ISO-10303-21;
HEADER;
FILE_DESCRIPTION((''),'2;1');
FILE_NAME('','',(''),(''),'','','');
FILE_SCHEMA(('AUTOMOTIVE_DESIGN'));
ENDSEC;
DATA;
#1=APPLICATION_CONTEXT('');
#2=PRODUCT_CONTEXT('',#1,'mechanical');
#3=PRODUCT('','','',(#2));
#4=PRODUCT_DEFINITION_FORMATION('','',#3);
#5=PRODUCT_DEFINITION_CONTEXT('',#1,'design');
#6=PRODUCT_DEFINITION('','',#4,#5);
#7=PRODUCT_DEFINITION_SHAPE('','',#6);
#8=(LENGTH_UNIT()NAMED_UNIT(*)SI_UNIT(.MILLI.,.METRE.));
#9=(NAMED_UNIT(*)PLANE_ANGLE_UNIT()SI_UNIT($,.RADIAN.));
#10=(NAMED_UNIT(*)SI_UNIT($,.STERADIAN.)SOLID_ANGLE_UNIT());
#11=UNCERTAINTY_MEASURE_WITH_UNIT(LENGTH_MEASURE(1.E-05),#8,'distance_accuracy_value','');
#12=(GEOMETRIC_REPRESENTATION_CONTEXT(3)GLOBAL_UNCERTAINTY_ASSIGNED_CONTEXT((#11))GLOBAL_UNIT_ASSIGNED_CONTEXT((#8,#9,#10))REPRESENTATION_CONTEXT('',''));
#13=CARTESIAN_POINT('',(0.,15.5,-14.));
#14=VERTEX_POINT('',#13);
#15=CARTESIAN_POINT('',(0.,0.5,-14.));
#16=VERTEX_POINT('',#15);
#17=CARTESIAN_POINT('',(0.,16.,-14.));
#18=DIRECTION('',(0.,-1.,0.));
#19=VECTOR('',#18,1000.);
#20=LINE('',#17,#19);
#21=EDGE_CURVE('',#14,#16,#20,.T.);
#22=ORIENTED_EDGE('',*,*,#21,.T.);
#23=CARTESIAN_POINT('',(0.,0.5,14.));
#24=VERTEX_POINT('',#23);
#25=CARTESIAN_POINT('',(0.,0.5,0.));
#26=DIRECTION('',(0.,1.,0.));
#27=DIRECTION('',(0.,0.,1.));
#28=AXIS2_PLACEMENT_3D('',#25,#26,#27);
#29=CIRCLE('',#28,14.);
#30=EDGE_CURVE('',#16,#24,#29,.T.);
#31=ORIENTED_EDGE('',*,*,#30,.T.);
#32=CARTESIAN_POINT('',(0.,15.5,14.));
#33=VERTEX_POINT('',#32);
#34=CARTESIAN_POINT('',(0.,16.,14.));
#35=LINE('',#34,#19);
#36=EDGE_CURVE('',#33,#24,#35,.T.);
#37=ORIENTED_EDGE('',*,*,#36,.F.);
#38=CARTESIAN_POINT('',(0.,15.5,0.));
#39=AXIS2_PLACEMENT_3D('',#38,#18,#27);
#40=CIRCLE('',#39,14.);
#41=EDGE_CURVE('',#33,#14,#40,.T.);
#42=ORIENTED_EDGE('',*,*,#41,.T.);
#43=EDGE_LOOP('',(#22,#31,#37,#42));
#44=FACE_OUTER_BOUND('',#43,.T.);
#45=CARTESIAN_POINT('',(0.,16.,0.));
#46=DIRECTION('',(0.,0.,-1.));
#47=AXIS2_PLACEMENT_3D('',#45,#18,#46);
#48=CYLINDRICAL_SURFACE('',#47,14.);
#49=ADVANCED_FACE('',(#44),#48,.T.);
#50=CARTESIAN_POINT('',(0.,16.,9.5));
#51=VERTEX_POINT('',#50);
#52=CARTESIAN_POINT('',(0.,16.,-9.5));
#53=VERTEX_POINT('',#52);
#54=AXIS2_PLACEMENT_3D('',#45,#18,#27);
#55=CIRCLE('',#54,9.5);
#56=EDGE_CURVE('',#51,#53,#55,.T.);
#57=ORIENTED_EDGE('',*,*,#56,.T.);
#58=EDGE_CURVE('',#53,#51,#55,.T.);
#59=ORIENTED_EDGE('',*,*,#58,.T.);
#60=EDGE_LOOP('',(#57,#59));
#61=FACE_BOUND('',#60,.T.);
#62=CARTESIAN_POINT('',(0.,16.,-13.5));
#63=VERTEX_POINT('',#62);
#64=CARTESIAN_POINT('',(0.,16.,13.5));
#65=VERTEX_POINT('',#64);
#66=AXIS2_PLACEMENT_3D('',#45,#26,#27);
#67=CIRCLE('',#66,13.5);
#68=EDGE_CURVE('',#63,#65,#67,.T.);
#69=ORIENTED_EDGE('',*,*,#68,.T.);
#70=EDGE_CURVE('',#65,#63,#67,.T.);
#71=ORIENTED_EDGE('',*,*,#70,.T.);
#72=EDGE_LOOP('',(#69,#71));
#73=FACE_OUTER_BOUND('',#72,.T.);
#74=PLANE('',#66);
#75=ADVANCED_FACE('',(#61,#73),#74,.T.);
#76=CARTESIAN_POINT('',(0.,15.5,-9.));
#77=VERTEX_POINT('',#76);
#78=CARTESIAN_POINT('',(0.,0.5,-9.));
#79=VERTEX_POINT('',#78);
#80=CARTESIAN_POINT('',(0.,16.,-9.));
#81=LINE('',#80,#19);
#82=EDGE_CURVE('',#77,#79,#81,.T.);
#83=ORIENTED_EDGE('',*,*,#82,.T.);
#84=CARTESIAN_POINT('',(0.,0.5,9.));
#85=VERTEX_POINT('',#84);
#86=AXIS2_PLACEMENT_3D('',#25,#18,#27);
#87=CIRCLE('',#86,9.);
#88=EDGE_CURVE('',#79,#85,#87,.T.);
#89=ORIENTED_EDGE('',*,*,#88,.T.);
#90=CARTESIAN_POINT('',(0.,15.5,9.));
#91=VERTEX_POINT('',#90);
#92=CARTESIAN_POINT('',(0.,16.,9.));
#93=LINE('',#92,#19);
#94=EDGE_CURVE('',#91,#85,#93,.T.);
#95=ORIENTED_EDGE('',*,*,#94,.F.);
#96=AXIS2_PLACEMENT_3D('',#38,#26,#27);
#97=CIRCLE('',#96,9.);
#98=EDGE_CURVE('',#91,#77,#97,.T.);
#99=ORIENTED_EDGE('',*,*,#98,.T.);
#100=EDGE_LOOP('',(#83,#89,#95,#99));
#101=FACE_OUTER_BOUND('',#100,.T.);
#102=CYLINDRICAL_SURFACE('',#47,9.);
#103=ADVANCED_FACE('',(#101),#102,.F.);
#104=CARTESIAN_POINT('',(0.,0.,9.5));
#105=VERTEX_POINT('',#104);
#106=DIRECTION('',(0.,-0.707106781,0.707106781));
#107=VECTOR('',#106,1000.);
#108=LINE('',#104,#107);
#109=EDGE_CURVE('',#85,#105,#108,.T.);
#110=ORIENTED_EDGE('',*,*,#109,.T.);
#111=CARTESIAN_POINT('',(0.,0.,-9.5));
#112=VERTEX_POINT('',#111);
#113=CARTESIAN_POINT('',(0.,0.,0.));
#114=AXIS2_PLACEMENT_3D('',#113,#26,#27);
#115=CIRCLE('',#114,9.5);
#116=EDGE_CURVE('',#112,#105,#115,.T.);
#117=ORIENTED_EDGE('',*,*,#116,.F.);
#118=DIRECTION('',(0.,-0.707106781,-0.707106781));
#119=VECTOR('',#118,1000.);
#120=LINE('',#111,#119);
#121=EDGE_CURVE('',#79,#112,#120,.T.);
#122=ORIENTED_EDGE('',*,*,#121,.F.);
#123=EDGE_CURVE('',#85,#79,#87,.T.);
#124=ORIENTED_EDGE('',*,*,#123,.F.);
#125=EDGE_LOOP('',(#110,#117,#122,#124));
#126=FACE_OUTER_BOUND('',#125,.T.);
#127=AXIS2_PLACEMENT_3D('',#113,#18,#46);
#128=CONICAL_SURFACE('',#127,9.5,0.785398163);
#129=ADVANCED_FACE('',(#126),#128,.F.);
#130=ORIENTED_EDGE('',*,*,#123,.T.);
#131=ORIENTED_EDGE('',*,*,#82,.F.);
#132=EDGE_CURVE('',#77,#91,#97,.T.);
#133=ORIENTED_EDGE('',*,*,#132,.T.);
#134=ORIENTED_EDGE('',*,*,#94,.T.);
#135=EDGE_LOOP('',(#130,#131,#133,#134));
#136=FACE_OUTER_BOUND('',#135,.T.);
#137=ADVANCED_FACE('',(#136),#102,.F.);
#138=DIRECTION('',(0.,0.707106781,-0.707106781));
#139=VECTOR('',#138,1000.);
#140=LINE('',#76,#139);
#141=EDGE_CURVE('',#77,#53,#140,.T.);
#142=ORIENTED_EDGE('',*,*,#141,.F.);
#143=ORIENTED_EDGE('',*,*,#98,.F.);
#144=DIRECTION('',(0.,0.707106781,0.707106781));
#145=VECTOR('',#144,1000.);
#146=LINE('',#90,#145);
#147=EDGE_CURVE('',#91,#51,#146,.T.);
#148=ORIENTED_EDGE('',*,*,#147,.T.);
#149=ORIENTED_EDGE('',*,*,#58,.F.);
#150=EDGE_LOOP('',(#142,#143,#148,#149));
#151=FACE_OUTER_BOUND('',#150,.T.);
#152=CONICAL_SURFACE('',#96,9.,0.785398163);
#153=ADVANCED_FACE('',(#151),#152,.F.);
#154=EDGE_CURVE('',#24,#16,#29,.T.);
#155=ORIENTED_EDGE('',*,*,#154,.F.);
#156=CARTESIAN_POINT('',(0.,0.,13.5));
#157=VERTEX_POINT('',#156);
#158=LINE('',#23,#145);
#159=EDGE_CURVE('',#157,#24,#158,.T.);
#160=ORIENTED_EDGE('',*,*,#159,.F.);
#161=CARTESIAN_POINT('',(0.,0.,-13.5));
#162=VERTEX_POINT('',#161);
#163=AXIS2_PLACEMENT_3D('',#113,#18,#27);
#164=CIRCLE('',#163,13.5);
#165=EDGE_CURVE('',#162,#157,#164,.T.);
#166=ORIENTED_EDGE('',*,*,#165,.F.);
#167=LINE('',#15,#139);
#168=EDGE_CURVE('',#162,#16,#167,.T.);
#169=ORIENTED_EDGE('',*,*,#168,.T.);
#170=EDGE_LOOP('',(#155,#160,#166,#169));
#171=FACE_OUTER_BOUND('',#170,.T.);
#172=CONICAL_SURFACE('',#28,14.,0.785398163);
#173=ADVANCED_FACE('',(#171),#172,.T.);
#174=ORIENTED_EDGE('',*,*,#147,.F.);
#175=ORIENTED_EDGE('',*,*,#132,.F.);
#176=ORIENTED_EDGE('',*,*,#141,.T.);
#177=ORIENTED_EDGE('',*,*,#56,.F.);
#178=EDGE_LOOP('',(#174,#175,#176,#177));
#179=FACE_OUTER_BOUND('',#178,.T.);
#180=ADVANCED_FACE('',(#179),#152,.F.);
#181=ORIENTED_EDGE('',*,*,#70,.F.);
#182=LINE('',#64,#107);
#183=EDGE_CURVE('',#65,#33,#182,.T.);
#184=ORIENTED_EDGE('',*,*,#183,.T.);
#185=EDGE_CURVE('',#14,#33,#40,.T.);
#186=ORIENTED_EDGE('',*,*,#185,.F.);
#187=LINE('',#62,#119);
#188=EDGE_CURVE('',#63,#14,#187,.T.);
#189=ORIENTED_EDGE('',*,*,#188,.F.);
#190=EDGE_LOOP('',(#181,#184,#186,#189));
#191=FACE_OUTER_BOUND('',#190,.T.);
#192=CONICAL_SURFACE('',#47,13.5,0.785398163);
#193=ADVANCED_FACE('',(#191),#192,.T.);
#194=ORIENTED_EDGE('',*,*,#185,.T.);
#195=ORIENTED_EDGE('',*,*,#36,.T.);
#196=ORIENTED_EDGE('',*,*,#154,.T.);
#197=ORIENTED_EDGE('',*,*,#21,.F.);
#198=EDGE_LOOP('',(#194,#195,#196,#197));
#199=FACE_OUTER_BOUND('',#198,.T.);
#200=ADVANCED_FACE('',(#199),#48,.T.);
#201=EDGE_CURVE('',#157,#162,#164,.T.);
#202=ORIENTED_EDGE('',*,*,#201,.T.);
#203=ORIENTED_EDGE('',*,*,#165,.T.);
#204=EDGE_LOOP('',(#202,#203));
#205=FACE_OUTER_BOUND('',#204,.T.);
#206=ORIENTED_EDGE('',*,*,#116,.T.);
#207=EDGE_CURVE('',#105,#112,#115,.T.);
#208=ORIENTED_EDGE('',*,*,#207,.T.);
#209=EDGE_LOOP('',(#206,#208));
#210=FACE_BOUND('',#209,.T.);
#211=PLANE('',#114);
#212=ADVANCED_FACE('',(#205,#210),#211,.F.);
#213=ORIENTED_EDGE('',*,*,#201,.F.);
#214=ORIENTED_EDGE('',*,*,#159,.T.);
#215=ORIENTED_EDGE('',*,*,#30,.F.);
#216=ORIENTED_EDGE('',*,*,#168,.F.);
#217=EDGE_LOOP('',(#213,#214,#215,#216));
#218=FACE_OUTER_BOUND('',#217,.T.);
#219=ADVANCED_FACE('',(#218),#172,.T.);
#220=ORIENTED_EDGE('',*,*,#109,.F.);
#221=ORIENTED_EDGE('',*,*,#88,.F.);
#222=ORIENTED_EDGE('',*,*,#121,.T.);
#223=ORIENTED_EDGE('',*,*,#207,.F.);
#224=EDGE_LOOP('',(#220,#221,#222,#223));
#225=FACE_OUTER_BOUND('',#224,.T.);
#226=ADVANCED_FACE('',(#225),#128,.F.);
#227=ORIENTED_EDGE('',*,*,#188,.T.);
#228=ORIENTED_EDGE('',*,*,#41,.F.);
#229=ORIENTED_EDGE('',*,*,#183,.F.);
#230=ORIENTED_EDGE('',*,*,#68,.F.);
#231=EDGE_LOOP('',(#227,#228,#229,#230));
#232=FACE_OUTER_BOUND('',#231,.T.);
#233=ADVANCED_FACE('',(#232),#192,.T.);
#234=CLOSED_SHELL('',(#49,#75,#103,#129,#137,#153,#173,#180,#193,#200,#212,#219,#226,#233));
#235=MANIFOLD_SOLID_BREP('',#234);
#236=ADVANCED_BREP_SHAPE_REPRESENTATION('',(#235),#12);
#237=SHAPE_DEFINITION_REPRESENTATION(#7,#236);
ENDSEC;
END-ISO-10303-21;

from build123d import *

# Parameters (mm, degrees)
SKETCH_1_R      = 14
SKETCH_1_R_2    = 9
EXTRUDE_1_DEPTH = 16
CHAMFER_1_SIZE  = 0.5


with BuildPart() as part:
    # 草图1 → 拉伸1 (new body)
    with BuildSketch(Plane(origin=(0, 0, 0), x_dir=(1, 0, 0), z_dir=(0, 1, 0))):
        with Locations(Location((0, 0, 0), (0, 0, 270))):
            Circle(SKETCH_1_R)
        with Locations(Location((0, 0, 0), (0, 0, 270))):
            Circle(SKETCH_1_R_2, mode=Mode.SUBTRACT)
    extrude(amount=EXTRUDE_1_DEPTH)

    # 倒角1
    chamfer_1_edges = [part.edges().sort_by_distance(p)[0] for p in [
        (0, 0, -14),
        (0, 16, -14),
        (0, 0, -9),
        (0, 16, -9),
    ]]
    chamfer(chamfer_1_edges, length=CHAMFER_1_SIZE)


solid = part.part
